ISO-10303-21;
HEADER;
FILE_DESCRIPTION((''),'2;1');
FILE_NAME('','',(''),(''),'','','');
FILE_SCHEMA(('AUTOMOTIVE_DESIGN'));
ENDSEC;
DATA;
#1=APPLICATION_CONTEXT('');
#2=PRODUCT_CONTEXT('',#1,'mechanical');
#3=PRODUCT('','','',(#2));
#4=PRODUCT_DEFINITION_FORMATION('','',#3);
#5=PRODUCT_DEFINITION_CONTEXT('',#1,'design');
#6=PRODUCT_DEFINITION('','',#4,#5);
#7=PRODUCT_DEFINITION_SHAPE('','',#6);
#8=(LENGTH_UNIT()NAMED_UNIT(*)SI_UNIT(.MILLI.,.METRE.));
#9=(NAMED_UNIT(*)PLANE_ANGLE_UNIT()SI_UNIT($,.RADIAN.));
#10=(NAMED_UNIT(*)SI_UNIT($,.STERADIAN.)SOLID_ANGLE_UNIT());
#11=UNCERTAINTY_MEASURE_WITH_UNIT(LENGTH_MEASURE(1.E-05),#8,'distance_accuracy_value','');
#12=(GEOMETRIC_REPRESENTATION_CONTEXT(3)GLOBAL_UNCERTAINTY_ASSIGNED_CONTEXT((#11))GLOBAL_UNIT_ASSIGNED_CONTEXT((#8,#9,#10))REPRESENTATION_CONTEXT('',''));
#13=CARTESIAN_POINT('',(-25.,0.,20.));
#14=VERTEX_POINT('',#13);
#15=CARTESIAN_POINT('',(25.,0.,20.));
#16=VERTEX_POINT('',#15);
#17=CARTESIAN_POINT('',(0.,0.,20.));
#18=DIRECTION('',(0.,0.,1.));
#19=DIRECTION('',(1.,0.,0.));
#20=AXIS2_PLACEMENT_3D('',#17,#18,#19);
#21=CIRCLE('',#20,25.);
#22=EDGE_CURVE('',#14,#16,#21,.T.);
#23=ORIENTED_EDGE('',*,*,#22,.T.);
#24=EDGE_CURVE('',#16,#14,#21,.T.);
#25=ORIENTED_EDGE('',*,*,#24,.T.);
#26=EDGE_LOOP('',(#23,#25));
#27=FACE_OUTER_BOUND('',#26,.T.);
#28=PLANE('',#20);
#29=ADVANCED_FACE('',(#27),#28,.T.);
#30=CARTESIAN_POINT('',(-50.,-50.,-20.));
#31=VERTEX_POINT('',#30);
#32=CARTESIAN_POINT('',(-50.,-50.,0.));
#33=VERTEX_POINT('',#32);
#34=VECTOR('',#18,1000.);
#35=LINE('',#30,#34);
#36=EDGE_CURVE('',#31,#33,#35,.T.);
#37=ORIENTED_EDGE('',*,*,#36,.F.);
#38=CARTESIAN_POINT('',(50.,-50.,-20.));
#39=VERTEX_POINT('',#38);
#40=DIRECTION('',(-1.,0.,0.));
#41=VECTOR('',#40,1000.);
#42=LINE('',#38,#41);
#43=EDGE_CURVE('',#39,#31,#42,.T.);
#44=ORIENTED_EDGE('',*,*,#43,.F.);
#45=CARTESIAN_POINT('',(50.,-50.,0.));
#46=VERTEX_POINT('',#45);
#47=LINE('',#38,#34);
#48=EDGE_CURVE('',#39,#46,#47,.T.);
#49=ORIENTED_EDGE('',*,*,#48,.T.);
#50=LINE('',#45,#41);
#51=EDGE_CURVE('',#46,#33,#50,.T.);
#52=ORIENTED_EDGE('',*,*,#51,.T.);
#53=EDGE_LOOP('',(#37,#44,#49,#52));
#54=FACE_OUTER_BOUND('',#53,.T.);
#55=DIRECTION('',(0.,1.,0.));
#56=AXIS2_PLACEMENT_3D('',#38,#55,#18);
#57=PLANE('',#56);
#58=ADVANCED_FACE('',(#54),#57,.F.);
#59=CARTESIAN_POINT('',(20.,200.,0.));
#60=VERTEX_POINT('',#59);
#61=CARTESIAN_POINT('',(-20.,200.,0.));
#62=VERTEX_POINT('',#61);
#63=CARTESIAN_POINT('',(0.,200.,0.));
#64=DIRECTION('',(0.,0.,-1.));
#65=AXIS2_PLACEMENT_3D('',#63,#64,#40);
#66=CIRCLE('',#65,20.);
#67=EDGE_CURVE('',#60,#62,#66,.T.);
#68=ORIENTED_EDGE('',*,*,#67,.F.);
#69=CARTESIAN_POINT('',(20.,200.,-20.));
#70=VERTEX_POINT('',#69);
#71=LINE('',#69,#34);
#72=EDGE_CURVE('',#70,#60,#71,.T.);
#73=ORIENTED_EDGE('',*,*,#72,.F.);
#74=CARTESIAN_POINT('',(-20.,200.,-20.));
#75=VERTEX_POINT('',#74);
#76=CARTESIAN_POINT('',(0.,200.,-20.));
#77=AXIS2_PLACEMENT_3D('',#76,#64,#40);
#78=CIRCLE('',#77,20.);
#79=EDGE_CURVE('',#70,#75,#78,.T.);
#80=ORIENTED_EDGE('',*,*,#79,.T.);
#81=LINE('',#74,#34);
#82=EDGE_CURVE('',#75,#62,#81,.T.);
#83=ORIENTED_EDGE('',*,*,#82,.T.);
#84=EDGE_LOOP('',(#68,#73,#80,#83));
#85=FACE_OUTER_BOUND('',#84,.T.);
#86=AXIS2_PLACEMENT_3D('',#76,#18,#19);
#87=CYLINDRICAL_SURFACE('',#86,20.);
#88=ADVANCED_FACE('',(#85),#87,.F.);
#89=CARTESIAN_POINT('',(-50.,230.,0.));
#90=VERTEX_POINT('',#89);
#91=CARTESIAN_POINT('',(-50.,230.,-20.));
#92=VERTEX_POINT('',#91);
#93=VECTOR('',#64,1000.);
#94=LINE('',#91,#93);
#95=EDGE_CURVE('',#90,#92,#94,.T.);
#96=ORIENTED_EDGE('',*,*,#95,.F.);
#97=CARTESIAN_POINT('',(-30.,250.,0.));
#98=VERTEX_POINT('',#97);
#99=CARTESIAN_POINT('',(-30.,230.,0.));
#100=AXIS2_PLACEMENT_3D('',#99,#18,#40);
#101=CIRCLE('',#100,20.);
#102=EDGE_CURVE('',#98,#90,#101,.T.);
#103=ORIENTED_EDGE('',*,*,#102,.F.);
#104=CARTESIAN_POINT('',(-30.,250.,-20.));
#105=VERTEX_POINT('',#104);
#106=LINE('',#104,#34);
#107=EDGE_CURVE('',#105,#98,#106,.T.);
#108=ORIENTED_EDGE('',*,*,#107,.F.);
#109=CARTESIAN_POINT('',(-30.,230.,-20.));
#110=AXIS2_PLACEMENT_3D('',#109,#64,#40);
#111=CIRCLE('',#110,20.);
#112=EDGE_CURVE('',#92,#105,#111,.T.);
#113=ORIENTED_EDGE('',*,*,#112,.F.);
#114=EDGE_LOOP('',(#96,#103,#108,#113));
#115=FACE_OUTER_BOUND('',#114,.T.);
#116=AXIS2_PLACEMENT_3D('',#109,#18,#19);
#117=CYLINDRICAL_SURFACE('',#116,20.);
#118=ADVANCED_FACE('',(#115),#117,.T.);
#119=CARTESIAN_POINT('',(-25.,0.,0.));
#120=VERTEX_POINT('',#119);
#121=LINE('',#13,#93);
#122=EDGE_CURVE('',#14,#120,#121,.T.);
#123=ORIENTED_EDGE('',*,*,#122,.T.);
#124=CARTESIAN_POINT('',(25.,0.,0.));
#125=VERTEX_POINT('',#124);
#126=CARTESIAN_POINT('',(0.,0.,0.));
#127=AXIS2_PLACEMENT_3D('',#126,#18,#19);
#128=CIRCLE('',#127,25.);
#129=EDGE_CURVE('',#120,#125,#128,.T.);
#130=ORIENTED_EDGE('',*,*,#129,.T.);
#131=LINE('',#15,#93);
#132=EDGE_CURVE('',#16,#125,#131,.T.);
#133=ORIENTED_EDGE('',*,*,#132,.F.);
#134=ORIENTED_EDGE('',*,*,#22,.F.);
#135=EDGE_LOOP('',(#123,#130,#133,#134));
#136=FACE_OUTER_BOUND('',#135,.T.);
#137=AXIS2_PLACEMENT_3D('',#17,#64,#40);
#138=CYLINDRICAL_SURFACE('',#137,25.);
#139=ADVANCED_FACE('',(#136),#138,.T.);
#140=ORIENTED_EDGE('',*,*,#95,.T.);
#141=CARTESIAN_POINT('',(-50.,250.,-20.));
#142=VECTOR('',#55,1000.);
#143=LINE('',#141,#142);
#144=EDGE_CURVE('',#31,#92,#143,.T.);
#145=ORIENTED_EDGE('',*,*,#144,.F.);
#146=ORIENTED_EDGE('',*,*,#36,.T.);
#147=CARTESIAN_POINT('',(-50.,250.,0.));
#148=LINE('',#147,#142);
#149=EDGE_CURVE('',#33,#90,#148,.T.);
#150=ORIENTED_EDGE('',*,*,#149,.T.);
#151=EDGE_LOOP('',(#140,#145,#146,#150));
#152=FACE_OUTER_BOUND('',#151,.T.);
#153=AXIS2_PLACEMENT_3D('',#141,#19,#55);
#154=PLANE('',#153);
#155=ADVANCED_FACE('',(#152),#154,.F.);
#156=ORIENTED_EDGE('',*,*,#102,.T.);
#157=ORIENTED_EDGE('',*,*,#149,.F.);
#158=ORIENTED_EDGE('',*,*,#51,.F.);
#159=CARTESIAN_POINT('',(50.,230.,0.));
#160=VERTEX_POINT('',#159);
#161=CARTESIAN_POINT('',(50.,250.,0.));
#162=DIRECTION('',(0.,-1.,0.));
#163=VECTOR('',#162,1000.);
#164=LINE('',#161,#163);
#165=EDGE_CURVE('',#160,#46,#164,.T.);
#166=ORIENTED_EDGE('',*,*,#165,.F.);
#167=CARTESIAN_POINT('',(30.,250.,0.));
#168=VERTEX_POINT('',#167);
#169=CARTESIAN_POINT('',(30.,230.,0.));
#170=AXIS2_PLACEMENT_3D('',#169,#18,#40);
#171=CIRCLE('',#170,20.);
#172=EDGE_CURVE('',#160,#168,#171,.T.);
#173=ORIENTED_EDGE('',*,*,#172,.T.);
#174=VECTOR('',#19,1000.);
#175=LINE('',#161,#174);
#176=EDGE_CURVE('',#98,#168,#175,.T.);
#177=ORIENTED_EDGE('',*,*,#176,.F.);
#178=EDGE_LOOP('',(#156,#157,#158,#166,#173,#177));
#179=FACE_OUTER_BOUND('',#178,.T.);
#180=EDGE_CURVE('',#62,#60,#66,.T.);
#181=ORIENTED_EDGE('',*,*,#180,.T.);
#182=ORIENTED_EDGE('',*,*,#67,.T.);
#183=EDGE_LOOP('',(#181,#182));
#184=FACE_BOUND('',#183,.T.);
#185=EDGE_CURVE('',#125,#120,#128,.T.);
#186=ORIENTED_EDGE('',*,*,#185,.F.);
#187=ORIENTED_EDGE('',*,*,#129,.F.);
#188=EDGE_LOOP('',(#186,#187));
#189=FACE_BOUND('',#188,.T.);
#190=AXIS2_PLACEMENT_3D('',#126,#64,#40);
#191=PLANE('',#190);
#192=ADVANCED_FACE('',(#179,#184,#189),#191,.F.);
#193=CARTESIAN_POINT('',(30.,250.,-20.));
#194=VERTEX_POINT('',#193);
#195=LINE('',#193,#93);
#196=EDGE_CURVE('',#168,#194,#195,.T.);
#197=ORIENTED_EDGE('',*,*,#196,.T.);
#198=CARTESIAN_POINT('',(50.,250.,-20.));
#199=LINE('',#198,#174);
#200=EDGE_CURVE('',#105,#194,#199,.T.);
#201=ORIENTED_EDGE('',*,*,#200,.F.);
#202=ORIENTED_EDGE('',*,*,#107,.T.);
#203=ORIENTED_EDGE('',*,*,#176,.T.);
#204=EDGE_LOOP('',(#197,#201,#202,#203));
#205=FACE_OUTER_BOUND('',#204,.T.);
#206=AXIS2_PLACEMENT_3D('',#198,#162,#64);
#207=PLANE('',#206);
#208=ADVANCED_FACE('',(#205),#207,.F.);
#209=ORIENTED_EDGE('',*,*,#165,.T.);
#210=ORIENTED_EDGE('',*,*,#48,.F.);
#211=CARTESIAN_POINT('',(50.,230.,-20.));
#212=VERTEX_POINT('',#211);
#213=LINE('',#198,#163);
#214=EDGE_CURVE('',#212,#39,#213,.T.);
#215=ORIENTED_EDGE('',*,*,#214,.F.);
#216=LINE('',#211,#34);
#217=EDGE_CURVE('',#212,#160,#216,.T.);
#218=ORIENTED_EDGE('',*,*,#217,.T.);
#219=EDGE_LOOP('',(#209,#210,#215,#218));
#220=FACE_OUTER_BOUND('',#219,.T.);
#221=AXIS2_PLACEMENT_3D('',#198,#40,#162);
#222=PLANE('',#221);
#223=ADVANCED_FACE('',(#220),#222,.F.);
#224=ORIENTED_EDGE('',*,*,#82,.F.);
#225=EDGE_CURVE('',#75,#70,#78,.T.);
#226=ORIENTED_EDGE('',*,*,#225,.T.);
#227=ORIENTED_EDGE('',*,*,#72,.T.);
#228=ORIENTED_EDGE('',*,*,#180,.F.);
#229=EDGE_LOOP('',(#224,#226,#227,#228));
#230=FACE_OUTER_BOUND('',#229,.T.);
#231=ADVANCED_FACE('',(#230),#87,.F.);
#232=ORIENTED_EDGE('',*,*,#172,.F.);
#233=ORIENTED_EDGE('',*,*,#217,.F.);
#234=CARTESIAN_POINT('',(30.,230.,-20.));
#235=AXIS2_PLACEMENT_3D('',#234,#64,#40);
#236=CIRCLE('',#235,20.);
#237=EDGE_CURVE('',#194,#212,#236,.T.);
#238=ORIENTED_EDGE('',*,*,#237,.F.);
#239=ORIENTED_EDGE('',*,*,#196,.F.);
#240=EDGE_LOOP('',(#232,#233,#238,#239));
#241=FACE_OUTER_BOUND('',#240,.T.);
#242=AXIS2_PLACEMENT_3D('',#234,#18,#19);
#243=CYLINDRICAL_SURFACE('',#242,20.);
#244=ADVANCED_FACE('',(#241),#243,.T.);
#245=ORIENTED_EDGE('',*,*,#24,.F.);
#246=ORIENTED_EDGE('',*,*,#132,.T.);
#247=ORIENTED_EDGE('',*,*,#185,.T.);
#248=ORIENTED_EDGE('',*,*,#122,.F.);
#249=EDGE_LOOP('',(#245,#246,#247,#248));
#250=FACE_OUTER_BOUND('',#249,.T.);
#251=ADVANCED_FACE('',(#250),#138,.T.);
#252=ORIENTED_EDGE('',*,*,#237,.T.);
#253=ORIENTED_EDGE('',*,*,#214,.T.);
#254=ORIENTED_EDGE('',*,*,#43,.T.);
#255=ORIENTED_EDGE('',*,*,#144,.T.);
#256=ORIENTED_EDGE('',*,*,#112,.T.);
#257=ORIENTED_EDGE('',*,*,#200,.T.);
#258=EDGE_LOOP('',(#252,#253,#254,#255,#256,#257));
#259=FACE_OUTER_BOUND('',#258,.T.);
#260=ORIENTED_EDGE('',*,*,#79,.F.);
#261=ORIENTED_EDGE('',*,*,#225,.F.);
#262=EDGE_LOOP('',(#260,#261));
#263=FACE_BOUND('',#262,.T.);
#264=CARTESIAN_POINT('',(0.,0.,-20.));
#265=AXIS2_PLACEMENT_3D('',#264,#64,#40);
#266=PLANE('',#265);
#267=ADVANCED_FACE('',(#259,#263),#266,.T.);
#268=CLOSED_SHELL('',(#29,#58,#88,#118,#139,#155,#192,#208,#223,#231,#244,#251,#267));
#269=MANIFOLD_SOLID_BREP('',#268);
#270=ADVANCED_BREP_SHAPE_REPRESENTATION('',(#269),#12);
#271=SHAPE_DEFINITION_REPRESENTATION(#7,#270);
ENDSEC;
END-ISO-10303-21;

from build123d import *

# Parameters (mm, degrees)
SKETCH_1_R      = 25
EXTRUDE_1_DEPTH = 20
SKETCH_2_W      = 100
SKETCH_2_H      = 300
SKETCH_2_R      = 20
EXTRUDE_2_DEPTH = 20
FILLET_1_R      = 20


with BuildPart() as part:
    # 草图1 → 凸台-拉伸1 (new body)
    with BuildSketch(Plane.XY):
        Circle(SKETCH_1_R)
    extrude(amount=EXTRUDE_1_DEPTH)

    # 草图2 → 凸台-拉伸2 (add)
    with BuildSketch(Plane(origin=(0, 0, 0), x_dir=(-1, 0, 0), z_dir=(0, 0, -1))):
        with Locations((0, 100)):
            Rectangle(SKETCH_2_W, SKETCH_2_H)
        with Locations((0, 200)):
            Circle(SKETCH_2_R, mode=Mode.SUBTRACT)
    extrude(amount=EXTRUDE_2_DEPTH)

    # 圆角1
    fillet_1_edges = [part.edges().sort_by_distance(p)[0] for p in [
        (-50, 250, -10),
        (50, 250, -10),
    ]]
    fillet(fillet_1_edges, radius=FILLET_1_R)


solid = part.part
